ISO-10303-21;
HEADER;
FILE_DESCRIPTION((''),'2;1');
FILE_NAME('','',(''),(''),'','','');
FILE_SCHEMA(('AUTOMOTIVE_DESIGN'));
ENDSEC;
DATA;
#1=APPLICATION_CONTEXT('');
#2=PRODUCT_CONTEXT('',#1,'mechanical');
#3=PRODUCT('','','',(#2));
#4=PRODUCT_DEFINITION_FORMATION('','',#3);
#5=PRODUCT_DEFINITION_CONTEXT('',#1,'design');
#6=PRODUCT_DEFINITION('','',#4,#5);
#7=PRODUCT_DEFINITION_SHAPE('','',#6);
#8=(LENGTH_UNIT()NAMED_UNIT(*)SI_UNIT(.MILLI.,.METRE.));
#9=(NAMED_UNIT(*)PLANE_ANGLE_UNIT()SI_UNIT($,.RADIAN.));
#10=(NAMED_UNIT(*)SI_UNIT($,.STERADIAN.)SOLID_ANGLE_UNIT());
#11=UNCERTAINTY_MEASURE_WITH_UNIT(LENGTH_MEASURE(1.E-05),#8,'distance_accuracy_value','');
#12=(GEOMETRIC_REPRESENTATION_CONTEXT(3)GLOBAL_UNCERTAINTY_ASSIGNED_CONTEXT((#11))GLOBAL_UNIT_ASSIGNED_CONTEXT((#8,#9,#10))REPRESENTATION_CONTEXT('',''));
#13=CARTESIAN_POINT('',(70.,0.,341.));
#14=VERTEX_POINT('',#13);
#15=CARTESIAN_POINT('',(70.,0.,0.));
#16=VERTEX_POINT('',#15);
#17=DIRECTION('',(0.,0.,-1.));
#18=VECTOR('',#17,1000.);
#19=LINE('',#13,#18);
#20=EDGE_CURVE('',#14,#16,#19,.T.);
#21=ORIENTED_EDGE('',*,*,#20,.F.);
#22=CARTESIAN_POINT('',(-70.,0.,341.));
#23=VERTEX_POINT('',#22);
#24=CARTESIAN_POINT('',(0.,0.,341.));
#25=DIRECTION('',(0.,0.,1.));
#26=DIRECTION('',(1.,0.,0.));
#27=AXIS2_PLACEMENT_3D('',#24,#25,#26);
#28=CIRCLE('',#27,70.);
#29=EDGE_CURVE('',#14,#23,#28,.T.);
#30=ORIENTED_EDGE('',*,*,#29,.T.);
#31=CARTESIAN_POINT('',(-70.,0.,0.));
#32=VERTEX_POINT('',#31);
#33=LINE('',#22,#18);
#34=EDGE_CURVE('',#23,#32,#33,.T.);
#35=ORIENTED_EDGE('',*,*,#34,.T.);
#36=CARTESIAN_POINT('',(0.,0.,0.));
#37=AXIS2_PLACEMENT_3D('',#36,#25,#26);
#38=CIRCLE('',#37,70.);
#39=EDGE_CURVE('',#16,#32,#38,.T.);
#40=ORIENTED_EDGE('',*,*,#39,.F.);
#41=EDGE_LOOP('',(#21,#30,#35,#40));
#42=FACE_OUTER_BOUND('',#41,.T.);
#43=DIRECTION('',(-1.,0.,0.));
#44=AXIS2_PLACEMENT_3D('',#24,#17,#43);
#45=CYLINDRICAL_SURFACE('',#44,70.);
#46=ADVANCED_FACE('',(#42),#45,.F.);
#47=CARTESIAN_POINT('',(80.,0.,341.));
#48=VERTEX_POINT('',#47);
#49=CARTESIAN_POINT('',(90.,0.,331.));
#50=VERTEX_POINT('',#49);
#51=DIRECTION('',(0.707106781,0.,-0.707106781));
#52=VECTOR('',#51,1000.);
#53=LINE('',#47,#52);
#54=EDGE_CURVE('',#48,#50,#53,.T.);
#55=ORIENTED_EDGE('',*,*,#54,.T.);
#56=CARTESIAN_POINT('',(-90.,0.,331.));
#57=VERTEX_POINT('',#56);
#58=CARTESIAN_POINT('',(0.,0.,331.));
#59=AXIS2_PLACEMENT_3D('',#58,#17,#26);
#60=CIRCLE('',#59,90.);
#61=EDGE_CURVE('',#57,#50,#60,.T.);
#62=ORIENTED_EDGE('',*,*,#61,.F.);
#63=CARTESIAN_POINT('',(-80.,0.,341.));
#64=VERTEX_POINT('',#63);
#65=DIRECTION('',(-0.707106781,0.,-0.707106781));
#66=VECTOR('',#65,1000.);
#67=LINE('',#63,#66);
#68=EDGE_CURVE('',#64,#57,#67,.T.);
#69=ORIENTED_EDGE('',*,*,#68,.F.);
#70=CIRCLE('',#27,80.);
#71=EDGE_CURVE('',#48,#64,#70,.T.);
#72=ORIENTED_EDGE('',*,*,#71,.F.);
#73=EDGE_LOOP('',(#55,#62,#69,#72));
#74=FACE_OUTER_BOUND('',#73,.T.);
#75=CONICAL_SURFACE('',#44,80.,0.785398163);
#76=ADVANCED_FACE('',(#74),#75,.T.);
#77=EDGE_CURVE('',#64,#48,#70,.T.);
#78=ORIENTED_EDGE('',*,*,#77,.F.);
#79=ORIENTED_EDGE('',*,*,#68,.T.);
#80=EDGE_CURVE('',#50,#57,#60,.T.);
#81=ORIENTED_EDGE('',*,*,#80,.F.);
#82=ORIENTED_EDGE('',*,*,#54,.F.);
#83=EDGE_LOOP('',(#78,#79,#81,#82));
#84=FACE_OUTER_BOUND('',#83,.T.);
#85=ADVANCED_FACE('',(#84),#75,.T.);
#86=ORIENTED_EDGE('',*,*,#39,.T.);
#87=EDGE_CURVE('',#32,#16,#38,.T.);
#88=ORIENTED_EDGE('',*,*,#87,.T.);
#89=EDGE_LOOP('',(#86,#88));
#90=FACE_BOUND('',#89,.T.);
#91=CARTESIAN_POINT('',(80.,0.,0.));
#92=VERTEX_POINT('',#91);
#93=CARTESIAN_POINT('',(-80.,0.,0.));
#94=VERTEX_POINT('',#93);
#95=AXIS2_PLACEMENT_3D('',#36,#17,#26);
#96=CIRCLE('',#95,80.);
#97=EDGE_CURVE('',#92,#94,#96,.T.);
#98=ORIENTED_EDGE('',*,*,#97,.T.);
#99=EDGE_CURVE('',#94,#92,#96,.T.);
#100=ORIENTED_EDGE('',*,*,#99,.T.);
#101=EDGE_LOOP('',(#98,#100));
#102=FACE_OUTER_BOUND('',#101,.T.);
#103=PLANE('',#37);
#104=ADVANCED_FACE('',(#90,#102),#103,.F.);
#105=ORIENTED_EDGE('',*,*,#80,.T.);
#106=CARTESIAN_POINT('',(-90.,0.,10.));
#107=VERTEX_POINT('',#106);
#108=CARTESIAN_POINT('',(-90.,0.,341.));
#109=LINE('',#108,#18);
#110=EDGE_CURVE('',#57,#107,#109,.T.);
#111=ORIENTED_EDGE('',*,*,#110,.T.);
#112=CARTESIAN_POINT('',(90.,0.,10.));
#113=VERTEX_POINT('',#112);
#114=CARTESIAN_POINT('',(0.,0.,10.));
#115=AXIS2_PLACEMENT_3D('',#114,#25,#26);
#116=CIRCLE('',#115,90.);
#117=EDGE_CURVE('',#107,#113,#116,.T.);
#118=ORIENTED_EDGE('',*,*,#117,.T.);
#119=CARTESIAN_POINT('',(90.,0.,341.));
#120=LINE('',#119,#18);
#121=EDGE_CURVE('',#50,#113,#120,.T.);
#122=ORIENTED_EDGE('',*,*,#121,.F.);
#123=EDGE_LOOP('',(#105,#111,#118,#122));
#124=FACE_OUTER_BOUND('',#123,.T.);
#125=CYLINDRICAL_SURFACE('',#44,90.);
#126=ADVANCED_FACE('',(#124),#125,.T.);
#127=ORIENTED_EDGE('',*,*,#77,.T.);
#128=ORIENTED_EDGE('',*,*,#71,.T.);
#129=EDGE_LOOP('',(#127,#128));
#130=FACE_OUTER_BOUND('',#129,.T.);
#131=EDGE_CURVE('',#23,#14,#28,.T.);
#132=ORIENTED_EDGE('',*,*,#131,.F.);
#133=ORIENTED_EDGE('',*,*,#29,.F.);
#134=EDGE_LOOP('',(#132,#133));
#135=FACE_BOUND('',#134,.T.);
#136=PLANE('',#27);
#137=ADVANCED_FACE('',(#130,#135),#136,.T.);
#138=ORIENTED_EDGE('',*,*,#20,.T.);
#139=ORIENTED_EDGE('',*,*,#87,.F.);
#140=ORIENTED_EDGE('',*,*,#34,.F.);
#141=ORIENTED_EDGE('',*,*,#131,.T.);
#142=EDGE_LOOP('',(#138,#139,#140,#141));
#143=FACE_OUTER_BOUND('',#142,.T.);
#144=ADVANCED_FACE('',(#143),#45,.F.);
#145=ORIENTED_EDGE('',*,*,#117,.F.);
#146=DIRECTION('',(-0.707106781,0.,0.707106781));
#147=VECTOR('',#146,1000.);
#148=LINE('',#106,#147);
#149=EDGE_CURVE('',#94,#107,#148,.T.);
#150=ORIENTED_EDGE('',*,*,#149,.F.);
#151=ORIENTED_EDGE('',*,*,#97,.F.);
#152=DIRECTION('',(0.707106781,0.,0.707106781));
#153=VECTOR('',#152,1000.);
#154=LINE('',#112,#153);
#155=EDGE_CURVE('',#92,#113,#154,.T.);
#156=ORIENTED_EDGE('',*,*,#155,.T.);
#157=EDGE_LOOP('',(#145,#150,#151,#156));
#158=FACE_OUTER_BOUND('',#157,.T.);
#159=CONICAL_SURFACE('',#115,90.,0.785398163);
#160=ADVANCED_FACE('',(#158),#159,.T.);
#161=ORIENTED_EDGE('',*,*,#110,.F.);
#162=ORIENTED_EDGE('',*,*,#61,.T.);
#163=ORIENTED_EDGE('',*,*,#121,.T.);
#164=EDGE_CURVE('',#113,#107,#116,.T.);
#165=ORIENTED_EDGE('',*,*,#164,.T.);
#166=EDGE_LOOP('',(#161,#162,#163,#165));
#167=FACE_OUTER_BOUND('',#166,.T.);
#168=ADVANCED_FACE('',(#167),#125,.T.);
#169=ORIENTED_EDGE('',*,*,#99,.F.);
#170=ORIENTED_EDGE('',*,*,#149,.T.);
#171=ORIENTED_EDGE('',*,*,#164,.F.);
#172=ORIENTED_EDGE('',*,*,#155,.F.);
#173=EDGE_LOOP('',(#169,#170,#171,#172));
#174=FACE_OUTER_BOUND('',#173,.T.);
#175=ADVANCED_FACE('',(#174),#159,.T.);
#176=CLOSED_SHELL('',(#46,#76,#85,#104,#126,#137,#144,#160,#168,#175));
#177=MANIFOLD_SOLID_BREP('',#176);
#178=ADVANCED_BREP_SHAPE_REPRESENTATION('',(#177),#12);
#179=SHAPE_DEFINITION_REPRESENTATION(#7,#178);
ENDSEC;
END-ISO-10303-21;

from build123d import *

# Parameters (mm, degrees)
SKETCH2_R           = 90
SKETCH2_R_2         = 70
BOSS_EXTRUDE1_DEPTH = 341
CHAMFER1_SIZE       = 10


with BuildPart() as part:
    # Sketch2 → Boss-Extrude1 (new body)
    with BuildSketch(Plane.XY):
        with Locations(Location((0, 0, 0), (0, 0, 180))):
            Circle(SKETCH2_R)
        with Locations(Location((0, 0, 0), (0, 0, 180))):
            Circle(SKETCH2_R_2, mode=Mode.SUBTRACT)
    extrude(amount=BOSS_EXTRUDE1_DEPTH)

    # Chamfer1
    chamfer1_edges = [part.edges().sort_by_distance(p)[0] for p in [
        (90, 0, 0),
        (90, 0, 341),
    ]]
    chamfer(chamfer1_edges, length=CHAMFER1_SIZE)


solid = part.part
